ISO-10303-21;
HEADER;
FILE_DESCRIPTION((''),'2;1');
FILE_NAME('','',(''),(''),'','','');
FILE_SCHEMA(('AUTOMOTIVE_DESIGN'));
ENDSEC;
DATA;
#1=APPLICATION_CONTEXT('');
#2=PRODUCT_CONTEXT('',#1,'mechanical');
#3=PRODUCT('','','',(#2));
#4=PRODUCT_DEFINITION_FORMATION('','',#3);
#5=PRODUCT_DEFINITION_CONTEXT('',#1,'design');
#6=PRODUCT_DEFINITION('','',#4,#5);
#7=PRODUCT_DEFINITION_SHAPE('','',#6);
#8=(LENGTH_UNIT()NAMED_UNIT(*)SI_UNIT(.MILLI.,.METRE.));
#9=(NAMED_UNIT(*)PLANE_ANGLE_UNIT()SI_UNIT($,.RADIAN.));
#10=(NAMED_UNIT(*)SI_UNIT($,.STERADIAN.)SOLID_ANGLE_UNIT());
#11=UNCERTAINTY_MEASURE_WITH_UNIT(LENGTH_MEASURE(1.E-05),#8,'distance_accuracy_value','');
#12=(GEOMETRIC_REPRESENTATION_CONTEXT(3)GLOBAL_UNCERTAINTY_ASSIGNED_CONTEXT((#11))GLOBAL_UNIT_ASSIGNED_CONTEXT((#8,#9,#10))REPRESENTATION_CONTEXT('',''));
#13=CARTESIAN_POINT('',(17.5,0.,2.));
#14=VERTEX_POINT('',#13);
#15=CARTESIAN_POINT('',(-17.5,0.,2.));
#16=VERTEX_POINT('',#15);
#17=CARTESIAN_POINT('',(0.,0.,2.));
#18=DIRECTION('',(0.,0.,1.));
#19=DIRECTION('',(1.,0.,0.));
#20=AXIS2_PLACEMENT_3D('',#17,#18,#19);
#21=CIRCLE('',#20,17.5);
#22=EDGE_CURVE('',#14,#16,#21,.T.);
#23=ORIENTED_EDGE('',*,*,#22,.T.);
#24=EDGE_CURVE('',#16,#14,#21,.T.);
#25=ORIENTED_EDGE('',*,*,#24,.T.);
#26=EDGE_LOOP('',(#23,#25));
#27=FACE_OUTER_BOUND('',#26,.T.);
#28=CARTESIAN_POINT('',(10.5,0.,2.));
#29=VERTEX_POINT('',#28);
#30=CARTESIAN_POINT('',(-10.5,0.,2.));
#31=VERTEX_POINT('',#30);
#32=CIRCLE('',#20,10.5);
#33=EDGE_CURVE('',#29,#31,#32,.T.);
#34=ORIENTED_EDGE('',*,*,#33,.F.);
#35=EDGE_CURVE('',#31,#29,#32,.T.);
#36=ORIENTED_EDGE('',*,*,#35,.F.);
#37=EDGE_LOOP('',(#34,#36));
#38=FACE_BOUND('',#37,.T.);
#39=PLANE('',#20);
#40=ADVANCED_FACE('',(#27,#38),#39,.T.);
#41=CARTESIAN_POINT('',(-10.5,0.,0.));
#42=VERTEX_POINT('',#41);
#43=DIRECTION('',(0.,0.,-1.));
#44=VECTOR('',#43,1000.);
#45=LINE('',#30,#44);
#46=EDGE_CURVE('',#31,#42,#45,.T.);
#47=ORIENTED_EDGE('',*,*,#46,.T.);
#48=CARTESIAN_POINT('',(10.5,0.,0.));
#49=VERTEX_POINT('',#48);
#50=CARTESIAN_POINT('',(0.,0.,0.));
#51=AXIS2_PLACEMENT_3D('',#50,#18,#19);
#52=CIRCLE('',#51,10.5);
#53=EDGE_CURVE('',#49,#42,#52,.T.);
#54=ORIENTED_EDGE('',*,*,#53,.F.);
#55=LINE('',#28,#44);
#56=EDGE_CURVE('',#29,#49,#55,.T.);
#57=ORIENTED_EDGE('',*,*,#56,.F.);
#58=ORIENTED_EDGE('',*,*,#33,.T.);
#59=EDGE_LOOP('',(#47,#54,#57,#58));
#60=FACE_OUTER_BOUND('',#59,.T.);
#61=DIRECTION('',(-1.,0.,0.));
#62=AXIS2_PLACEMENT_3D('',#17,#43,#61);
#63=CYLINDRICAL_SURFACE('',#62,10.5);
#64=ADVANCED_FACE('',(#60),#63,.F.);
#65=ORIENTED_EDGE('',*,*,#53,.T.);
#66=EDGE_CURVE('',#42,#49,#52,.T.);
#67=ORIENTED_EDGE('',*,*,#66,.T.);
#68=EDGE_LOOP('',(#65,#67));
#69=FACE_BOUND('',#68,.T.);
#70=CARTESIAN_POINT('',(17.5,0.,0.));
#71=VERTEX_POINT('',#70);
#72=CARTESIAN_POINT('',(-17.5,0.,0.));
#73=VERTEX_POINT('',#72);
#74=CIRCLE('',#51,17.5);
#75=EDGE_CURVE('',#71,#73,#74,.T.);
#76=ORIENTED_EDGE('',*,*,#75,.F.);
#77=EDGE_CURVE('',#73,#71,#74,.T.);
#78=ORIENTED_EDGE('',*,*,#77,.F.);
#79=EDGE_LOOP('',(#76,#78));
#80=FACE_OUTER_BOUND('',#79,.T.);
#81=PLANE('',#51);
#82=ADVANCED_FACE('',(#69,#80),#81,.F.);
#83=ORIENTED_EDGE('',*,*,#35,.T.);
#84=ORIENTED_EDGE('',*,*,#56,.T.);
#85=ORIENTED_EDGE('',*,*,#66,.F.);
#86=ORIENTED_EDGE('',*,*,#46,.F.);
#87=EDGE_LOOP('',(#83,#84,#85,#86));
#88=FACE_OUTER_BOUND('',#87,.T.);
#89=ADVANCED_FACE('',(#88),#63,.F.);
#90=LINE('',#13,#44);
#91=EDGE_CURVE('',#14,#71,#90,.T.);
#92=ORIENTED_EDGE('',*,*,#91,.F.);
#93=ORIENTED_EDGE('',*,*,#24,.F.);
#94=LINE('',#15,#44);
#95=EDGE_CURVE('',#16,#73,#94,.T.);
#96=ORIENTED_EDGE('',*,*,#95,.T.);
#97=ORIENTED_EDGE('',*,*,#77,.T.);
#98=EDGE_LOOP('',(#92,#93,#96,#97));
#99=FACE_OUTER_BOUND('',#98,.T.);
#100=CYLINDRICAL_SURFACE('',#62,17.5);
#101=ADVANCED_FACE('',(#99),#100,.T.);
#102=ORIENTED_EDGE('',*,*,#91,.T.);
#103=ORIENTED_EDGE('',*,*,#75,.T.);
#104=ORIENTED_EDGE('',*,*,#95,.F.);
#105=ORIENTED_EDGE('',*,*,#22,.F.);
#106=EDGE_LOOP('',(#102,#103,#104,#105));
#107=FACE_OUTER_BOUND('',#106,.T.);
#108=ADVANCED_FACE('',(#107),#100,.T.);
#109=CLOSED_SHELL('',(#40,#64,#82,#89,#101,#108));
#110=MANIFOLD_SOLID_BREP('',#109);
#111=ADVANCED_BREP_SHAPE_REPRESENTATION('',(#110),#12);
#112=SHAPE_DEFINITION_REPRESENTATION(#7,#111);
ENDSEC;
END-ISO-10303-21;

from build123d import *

# Parameters (mm, degrees)
SKETCH_1_R      = 17.5
SKETCH_1_R_2    = 10.5
EXTRUDE_1_DEPTH = 2


with BuildPart() as part:
    # 草图1 → 凸台-拉伸1 (new body)
    with BuildSketch(Plane.XY):
        Circle(SKETCH_1_R)
        Circle(SKETCH_1_R_2, mode=Mode.SUBTRACT)
    extrude(amount=EXTRUDE_1_DEPTH)


solid = part.part
